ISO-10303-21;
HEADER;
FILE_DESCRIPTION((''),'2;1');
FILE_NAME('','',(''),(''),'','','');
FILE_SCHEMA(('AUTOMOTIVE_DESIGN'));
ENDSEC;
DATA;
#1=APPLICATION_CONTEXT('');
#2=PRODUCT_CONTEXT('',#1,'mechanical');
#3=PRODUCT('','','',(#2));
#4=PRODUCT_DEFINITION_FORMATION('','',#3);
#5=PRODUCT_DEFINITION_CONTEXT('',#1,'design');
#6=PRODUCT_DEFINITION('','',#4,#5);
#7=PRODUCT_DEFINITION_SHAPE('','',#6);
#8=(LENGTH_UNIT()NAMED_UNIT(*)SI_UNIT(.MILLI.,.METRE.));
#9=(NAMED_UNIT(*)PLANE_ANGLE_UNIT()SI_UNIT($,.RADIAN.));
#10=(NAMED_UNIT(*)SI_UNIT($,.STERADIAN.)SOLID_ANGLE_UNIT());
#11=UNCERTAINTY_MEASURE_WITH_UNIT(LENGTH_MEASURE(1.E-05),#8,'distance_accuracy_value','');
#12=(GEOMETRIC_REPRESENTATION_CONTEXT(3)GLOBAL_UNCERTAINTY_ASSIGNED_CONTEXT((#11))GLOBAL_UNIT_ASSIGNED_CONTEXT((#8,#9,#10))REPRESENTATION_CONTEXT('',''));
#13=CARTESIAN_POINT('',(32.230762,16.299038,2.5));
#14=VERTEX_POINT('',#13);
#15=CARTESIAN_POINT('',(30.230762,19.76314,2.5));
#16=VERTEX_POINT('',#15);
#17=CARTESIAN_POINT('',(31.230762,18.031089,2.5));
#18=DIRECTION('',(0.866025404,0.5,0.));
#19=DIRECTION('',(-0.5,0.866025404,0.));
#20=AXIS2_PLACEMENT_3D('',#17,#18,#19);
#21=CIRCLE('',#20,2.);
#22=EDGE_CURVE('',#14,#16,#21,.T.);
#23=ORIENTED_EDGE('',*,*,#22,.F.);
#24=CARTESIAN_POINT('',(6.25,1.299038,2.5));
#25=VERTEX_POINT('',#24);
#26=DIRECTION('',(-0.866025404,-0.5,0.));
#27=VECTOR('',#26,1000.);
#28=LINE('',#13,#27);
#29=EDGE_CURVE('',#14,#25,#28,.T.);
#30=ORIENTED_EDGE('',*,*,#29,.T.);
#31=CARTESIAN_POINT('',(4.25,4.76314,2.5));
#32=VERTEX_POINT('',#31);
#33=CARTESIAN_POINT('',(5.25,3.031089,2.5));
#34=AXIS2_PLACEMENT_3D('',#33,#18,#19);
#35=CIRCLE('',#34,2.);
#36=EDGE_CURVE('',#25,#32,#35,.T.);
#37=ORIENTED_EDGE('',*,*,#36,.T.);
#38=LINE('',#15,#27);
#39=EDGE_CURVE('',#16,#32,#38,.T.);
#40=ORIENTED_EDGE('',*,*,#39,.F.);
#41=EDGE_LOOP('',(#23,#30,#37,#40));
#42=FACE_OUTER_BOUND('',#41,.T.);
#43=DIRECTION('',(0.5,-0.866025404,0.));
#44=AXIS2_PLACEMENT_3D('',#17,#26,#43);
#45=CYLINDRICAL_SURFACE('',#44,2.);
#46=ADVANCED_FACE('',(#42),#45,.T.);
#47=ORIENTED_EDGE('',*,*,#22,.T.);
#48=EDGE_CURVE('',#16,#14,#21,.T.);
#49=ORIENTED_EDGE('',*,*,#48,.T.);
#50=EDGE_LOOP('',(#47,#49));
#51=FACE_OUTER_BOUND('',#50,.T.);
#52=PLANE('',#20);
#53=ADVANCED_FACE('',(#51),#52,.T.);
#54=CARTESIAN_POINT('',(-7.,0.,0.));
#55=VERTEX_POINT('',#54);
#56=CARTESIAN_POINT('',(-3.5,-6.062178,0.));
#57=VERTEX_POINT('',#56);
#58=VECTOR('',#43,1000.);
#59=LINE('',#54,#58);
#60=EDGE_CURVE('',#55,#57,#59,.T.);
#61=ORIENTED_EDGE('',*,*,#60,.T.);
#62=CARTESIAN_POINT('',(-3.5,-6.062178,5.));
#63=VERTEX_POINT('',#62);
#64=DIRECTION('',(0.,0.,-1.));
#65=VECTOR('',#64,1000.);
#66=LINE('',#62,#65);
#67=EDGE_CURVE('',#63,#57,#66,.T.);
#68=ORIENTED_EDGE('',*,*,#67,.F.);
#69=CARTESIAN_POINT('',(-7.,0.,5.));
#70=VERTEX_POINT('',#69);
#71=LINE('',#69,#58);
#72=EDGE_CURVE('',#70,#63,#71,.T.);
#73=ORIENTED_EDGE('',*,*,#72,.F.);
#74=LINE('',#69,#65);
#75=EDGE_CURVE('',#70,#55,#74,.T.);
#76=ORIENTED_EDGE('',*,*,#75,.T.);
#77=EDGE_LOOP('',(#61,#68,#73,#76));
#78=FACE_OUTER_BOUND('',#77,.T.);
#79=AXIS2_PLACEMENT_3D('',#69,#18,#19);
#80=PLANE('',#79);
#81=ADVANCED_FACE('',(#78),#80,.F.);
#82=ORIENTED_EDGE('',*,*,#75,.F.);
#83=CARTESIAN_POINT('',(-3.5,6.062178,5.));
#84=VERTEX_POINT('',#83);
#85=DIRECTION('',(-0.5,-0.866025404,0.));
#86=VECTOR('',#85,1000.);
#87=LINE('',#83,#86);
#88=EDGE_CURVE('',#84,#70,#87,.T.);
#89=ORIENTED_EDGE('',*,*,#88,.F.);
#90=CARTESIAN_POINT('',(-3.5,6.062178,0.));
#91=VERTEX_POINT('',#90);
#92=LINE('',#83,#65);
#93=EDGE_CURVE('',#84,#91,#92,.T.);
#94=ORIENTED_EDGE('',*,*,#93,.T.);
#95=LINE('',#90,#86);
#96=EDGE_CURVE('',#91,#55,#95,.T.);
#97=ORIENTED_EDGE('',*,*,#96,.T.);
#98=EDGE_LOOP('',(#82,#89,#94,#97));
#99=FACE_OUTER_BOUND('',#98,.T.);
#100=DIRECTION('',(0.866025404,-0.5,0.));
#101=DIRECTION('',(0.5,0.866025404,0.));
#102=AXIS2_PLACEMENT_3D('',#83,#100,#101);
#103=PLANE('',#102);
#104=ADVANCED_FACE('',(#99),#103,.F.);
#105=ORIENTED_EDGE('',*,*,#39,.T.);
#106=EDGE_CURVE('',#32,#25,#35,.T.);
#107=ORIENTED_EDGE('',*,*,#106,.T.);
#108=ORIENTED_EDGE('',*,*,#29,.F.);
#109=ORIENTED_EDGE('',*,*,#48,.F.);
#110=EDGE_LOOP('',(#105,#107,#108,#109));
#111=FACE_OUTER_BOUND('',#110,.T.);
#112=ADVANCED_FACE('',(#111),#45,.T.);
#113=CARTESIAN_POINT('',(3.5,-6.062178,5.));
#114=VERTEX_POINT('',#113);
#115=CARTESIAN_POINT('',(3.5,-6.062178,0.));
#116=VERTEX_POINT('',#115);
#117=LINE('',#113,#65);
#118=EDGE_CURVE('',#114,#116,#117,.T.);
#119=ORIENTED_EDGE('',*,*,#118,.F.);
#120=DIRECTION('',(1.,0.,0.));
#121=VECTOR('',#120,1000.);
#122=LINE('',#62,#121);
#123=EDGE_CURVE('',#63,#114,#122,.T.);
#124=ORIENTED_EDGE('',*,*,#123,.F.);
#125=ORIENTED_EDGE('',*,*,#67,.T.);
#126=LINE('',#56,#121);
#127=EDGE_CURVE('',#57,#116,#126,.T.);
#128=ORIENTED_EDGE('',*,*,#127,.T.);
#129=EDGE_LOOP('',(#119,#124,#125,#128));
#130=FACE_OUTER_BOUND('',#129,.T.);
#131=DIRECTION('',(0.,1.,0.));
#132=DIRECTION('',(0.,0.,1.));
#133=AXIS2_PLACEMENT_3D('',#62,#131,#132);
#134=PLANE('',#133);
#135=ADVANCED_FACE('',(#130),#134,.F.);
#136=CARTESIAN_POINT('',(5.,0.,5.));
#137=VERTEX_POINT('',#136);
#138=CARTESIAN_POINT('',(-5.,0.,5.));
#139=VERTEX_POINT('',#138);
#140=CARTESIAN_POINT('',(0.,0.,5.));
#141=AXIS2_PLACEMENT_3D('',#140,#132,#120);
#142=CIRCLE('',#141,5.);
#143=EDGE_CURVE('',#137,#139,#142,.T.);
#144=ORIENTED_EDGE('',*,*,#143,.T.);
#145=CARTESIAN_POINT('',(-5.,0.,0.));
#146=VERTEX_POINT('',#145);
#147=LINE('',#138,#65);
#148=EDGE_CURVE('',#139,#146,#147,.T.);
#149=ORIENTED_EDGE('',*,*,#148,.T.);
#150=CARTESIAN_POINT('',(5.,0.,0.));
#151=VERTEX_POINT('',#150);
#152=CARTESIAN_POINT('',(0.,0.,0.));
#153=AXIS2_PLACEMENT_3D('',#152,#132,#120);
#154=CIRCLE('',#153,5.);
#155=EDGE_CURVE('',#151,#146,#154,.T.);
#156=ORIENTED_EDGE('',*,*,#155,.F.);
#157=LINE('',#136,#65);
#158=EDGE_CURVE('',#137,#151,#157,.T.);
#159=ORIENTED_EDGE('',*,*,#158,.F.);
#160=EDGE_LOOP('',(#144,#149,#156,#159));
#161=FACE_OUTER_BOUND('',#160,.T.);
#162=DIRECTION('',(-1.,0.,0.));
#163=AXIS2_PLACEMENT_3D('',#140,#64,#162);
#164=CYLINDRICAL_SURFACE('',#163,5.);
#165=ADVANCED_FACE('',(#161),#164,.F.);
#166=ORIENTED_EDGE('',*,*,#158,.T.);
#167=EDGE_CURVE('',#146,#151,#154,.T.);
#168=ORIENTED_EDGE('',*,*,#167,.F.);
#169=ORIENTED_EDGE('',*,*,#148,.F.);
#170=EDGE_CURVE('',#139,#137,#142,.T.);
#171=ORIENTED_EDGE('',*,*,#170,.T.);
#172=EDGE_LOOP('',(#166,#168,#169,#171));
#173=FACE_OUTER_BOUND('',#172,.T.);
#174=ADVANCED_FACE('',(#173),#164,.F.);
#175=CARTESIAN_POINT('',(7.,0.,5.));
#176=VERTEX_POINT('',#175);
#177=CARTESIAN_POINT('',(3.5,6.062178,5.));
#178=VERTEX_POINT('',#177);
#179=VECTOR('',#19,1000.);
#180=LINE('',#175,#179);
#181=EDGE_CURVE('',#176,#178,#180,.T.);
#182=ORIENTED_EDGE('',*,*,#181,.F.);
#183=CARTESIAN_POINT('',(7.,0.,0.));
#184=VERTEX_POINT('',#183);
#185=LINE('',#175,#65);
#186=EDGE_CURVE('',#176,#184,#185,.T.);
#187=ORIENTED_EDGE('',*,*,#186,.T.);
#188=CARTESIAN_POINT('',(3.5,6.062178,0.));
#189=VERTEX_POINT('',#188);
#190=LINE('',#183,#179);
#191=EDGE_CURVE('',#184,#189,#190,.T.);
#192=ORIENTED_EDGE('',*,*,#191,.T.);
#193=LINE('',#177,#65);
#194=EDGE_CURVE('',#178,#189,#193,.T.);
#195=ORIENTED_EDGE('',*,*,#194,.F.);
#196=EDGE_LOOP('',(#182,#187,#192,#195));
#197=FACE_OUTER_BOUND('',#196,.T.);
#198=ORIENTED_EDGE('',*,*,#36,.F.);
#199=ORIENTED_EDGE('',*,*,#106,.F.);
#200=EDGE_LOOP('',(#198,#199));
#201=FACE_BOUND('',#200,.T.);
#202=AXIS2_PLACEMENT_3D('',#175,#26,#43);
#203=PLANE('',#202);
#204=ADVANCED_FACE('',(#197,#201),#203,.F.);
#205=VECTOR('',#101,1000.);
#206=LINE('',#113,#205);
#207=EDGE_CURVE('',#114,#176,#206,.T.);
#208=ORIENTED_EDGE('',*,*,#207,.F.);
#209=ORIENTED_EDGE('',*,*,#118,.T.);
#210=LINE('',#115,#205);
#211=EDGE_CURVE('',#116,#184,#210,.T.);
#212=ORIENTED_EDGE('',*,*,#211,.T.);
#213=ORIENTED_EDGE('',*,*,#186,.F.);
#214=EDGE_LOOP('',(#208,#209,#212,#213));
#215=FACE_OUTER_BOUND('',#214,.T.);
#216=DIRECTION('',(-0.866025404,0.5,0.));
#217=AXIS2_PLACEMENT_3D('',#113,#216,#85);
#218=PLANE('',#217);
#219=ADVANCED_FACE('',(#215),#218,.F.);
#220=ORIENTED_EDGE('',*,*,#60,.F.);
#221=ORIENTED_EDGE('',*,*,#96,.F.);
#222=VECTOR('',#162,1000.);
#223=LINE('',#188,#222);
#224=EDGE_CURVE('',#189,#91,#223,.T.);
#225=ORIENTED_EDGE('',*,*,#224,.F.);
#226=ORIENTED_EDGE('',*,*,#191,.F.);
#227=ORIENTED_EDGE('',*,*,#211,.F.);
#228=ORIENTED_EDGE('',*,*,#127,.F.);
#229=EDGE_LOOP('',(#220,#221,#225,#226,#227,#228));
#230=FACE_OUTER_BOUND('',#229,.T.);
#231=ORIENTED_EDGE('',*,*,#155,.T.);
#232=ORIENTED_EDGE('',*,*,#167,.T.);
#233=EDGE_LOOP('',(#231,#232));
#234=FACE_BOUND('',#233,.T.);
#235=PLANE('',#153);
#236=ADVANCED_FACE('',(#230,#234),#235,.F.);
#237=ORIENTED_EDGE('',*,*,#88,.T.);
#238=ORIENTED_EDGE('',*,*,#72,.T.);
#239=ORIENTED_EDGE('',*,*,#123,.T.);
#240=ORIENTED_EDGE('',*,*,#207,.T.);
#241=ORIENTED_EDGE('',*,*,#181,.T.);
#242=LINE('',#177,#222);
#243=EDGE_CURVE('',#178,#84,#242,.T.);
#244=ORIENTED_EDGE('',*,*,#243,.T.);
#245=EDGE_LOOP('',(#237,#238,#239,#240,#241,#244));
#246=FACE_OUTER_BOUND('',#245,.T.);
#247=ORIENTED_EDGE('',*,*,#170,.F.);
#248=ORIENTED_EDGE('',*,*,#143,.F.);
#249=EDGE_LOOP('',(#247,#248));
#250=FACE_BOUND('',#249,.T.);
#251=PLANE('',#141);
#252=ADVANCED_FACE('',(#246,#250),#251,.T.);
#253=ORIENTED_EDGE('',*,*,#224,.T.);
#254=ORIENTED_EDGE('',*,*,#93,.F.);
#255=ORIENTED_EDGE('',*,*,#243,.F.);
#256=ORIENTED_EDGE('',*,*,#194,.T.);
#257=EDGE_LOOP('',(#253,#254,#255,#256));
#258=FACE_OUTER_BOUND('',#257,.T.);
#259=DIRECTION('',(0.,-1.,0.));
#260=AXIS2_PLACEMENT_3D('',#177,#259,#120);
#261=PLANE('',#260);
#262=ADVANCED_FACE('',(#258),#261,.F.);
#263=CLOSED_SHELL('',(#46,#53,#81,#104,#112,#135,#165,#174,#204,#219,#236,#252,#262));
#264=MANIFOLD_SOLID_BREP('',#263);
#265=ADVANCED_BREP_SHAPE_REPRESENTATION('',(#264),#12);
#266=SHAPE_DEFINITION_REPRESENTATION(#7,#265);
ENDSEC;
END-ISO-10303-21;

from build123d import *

# Parameters (mm, degrees)
SKETCH1_R           = 5
BOSS_EXTRUDE1_DEPTH = 5
SKETCH2_R           = 2
BOSS_EXTRUDE2_DEPTH = 30


with BuildPart() as part:
    # Sketch1 → Boss-Extrude1 (new body)
    with BuildSketch(Plane.XY):
        Polygon((-3.5, 6.062177826), (-7, 0), (-3.5, -6.062177826), (3.5, -6.062177826), (7, 0), (3.5, 6.062177826), align=None)
        Circle(SKETCH1_R, mode=Mode.SUBTRACT)
    extrude(amount=BOSS_EXTRUDE1_DEPTH)

    # Sketch2 → Boss-Extrude2 (add)
    with BuildSketch(Plane(origin=(5.25, 3.031088913, 0), x_dir=(0, 0, -1), z_dir=(0.8660254037844387, 0.49999999999999983, 0))):
        with Locations(Location((-2.5, 0, 0), (0, 0, 90))):
            Circle(SKETCH2_R)
    extrude(amount=BOSS_EXTRUDE2_DEPTH)


solid = part.part
